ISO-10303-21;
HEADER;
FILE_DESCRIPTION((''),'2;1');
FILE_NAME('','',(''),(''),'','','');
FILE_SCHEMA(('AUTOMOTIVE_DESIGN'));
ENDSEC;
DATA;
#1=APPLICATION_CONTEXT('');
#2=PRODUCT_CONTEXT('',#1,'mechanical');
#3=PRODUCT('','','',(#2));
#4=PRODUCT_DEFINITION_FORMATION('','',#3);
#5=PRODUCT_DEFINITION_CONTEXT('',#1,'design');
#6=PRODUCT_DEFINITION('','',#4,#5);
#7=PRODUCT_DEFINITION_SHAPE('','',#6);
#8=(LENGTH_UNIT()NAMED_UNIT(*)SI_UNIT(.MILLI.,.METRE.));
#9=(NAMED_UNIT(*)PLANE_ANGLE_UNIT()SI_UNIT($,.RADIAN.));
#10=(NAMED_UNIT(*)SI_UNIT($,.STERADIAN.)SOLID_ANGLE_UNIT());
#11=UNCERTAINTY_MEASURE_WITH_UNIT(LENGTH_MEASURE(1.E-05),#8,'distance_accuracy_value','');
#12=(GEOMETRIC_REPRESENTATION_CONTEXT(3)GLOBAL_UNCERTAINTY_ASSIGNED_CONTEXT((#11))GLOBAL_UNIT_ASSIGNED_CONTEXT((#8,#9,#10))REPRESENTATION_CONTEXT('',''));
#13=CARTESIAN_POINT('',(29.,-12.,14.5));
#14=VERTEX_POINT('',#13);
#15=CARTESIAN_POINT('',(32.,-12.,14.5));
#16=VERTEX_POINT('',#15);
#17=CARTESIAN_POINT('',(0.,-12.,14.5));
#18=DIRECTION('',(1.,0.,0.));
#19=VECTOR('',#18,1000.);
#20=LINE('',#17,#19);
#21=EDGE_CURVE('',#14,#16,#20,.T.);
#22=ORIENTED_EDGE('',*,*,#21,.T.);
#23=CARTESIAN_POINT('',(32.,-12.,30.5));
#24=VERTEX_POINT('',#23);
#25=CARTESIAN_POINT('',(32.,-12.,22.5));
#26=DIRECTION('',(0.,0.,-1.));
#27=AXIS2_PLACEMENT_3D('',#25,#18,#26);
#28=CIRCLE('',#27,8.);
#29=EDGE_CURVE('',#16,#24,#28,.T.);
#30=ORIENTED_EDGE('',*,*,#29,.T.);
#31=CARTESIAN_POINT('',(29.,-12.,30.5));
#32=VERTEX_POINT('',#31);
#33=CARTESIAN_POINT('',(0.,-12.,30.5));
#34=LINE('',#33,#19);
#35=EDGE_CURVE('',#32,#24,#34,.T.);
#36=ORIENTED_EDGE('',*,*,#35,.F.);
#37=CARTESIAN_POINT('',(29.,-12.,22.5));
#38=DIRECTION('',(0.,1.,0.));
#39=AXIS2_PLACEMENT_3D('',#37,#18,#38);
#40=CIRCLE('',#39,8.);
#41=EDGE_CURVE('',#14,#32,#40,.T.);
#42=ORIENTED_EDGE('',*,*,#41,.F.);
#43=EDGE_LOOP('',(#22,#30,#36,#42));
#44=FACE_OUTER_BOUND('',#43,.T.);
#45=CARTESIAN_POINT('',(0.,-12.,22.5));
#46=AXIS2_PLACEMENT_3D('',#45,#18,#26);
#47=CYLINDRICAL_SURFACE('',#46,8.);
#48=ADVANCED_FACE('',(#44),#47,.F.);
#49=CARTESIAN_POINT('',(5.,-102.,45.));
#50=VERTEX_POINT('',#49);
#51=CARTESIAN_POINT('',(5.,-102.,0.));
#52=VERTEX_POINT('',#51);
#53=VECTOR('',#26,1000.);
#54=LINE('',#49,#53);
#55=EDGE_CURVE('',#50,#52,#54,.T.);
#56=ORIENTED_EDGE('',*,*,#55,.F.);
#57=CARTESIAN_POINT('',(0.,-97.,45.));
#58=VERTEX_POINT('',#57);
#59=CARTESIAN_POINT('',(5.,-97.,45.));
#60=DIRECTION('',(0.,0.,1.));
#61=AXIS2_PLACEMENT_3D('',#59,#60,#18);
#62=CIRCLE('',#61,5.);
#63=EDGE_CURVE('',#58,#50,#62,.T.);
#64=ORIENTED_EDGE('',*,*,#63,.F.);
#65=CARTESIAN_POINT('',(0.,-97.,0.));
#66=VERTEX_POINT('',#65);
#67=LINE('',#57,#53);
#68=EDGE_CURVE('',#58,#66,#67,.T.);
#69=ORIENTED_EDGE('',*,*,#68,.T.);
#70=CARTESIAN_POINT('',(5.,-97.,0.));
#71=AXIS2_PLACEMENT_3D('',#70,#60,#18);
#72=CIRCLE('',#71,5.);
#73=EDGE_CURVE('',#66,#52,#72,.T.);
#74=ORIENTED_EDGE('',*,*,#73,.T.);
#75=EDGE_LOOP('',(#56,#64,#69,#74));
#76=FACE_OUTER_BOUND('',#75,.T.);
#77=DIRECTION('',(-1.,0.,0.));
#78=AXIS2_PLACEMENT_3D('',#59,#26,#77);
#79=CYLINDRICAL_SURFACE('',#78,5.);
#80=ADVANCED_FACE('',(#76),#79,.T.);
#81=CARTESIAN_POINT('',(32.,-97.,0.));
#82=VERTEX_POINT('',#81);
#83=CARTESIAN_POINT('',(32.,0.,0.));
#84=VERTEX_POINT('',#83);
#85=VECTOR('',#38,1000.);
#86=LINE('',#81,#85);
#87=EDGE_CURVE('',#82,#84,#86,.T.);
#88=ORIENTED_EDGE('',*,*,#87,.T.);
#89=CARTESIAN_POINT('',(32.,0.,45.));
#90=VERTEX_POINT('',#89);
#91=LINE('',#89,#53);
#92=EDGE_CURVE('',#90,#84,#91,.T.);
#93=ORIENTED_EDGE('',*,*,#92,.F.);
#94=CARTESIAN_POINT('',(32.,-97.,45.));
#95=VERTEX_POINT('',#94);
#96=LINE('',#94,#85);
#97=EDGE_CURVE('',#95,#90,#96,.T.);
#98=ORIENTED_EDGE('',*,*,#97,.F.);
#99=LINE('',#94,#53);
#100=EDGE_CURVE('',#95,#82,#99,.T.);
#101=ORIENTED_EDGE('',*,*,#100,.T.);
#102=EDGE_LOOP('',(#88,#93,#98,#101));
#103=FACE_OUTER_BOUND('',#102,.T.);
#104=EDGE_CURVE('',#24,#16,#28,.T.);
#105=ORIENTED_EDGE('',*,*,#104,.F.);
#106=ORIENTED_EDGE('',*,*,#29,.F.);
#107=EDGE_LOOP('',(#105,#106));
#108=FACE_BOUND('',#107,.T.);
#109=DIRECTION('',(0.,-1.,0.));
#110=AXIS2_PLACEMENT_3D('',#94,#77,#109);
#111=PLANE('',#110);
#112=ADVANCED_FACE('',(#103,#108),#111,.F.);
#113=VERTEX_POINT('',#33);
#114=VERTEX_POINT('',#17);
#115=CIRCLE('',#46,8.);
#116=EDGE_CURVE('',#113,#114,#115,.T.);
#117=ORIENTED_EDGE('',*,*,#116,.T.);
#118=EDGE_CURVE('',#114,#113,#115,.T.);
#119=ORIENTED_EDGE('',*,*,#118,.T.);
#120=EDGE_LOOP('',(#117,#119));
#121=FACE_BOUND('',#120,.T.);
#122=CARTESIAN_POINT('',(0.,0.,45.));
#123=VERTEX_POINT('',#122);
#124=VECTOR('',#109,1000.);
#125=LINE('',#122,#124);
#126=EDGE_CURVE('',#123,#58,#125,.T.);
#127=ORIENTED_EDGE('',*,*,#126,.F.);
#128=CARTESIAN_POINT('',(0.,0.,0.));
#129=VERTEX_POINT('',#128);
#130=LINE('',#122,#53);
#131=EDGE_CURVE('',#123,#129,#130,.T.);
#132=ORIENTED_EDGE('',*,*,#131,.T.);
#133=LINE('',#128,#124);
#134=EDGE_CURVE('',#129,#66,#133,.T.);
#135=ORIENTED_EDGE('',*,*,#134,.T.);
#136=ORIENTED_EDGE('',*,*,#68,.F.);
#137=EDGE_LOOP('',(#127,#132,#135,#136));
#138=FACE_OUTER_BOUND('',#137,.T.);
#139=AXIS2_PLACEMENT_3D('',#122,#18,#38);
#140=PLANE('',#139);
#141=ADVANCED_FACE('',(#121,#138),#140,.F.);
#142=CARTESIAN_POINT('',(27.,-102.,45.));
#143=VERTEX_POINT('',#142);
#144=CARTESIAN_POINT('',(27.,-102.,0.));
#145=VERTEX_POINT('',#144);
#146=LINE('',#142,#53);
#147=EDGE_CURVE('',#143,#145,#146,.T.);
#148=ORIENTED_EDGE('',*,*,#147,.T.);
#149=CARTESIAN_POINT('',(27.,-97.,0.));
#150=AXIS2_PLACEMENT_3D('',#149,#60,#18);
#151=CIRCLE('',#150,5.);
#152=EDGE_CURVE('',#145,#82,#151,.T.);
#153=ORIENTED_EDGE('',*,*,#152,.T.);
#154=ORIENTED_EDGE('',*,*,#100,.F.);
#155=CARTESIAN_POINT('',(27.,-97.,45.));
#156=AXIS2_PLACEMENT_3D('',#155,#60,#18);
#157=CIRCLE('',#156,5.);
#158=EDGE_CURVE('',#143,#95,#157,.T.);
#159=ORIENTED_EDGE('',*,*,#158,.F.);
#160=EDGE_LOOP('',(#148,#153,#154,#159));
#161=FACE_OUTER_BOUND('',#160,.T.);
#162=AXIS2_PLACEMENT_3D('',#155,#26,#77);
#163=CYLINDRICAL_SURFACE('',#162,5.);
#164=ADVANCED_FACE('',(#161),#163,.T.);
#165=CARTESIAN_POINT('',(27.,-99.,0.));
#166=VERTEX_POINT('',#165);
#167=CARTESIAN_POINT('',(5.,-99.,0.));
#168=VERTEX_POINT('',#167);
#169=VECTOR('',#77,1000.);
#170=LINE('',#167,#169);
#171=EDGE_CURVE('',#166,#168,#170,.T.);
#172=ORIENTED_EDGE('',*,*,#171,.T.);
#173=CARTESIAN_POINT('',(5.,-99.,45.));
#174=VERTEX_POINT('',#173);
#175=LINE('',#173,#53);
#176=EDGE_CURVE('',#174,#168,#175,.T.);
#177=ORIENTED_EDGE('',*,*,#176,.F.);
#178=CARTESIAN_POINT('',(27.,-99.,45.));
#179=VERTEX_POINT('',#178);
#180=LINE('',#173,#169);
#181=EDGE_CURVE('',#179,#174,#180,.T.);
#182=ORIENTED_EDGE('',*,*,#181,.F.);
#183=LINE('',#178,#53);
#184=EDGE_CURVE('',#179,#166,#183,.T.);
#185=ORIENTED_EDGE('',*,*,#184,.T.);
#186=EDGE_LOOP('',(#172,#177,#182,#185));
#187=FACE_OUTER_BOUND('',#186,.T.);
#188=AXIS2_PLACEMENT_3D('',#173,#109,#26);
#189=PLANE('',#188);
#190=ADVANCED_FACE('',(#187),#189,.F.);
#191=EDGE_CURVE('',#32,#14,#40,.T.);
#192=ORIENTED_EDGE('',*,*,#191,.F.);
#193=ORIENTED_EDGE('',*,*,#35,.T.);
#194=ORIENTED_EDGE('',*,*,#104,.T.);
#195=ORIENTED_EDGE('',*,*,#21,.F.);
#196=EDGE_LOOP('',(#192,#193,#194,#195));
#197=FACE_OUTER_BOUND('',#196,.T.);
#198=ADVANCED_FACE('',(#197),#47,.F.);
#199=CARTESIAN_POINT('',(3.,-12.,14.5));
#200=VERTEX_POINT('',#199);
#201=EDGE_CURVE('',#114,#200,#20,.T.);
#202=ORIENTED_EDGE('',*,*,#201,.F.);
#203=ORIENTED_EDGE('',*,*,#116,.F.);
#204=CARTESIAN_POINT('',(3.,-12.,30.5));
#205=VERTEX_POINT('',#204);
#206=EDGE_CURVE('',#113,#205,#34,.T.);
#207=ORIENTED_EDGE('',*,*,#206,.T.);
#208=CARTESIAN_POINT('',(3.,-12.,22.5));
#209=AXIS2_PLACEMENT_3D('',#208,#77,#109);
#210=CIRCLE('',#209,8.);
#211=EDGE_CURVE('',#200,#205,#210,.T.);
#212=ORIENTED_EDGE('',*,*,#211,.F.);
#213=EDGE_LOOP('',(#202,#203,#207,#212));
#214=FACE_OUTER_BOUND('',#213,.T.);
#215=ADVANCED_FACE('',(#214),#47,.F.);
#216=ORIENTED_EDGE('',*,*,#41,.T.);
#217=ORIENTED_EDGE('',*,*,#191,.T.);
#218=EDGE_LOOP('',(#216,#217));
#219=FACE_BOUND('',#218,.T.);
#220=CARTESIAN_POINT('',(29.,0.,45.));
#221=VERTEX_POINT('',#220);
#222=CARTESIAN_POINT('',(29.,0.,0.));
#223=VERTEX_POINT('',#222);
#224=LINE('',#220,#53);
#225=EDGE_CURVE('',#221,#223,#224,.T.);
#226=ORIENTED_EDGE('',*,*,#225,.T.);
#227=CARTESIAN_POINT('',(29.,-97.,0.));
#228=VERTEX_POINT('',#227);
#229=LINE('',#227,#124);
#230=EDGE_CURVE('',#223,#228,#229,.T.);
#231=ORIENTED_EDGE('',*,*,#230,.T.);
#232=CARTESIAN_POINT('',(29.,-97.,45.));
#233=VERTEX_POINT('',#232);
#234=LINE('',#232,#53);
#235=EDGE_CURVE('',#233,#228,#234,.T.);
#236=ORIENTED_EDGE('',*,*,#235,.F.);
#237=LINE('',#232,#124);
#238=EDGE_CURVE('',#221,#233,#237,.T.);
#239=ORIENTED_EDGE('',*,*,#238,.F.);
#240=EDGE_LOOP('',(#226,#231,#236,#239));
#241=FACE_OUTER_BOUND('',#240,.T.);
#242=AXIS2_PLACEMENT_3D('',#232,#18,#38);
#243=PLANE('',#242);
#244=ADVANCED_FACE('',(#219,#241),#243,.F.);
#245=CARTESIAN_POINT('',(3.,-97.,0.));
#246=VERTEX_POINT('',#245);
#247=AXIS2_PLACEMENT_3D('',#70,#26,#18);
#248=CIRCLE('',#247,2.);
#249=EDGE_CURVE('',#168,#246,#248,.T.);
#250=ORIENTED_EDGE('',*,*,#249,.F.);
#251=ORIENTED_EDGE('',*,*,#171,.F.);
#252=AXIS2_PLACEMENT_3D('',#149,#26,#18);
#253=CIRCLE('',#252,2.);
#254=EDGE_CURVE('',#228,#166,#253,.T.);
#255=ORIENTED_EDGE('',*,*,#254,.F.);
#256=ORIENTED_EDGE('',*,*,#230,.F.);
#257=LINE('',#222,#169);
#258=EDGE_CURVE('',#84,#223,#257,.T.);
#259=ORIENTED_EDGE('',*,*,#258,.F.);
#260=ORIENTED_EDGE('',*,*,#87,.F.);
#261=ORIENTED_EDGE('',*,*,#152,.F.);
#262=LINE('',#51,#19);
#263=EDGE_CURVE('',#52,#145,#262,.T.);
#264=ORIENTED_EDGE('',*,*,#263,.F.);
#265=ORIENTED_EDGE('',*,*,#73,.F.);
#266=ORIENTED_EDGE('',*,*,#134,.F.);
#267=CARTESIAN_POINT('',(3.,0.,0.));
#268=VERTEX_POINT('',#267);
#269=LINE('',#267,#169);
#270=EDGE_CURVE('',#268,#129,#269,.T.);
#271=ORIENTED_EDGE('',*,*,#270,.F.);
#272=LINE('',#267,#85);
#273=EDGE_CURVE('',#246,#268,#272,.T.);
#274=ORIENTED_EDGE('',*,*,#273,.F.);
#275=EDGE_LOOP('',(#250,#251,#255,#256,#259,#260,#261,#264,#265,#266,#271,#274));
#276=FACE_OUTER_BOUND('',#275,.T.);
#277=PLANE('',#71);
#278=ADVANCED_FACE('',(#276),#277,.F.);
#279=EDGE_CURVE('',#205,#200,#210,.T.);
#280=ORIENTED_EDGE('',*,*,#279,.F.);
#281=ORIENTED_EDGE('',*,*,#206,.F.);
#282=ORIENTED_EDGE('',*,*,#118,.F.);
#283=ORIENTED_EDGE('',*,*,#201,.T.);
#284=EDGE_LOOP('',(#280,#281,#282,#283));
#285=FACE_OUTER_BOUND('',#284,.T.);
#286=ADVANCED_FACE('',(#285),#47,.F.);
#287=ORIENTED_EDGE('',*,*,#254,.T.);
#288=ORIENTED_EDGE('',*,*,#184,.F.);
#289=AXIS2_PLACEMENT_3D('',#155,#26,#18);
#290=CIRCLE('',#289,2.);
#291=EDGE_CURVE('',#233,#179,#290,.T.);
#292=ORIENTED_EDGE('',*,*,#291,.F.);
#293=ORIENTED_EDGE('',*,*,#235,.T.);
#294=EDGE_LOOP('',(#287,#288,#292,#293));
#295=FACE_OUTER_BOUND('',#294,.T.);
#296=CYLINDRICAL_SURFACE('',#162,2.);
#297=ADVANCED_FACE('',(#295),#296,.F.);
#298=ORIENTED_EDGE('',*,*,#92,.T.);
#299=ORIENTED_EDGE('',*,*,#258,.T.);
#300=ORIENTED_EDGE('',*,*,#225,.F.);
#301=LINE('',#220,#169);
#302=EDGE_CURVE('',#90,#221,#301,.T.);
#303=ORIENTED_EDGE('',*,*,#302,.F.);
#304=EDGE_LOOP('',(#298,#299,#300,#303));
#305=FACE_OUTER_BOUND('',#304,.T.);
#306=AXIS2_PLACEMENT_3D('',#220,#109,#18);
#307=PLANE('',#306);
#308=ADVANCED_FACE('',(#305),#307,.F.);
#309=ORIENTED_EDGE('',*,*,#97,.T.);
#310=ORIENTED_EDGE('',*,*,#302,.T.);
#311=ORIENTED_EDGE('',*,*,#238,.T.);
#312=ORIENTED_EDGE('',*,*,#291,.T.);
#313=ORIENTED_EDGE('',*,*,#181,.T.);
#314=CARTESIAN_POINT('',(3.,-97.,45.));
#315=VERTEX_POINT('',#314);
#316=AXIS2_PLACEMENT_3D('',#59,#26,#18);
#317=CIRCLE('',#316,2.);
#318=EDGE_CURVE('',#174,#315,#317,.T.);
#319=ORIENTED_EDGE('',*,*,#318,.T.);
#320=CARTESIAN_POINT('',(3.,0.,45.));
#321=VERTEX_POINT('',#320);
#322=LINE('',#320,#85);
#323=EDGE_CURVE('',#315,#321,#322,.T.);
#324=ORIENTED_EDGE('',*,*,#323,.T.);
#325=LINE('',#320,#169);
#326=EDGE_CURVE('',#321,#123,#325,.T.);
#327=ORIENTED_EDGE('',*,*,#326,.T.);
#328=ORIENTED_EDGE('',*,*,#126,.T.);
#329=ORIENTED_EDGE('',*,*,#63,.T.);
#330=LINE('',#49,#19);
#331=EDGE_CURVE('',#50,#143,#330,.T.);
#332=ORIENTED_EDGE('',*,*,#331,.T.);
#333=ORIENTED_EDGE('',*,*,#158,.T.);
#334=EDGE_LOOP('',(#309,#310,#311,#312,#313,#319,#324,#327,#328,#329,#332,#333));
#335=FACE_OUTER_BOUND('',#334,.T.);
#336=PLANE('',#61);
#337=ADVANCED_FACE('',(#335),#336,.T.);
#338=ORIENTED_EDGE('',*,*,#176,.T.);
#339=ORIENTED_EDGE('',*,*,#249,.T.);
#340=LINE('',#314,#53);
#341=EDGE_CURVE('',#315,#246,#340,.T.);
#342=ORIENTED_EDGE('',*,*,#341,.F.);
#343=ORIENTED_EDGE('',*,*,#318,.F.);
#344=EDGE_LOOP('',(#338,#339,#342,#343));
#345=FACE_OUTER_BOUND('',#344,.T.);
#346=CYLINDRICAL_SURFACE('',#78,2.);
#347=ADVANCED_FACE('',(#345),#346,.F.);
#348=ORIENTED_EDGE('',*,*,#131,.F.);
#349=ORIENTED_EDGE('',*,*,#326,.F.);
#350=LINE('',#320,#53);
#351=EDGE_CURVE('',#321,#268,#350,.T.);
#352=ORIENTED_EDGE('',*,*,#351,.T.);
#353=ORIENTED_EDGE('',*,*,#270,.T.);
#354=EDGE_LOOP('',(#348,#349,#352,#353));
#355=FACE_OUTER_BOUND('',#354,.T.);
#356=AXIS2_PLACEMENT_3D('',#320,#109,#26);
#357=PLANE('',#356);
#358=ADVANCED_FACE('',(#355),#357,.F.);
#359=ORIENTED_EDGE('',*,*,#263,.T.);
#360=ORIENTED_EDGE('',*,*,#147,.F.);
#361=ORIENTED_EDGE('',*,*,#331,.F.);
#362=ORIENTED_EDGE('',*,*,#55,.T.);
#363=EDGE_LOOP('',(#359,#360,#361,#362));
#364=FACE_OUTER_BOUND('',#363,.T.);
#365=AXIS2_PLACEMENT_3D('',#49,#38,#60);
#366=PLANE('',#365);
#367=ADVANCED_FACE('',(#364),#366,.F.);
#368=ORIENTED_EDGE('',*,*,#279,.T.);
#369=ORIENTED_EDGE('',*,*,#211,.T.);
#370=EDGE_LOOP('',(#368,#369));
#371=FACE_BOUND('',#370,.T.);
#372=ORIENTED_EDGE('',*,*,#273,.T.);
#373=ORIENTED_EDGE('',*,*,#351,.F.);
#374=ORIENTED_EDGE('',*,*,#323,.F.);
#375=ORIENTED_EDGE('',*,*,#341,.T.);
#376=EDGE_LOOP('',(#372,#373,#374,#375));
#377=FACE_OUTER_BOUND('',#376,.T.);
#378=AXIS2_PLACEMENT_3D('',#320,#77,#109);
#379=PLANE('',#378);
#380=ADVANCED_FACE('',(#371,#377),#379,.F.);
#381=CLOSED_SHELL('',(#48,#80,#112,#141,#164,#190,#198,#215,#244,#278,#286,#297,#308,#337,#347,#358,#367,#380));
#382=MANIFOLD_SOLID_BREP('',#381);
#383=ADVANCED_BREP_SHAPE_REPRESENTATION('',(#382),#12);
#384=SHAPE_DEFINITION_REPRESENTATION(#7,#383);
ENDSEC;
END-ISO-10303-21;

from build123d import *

# Parameters (mm, degrees)
BOSS_EXTRUDE1_DEPTH = 45
SKETCH2_R           = 8
CUT_EXTRUDE1_DEPTH  = 116.987068245


with BuildPart() as part:
    # Sketch1 → Boss-Extrude1 (new body)
    with BuildSketch(Plane.XY):
        with BuildLine():
            Line((0, 0), (0, -97))
            ThreePointArc((0, -97), (1.464466094, -100.535533906), (5, -102))
            Line((5, -102), (27, -102))
            ThreePointArc((27, -102), (30.535533906, -100.535533906), (32, -97))
            Line((32, -97), (32, 0))
            Line((32, 0), (29, 0))
            Line((29, 0), (29, -97))
            ThreePointArc((29, -97), (28.414213562, -98.414213562), (27, -99))
            Line((27, -99), (5, -99))
            ThreePointArc((5, -99), (3.585786438, -98.414213562), (3, -97))
            Line((3, -97), (3, 0))
            Line((3, 0), (0, 0))
        make_face()
    extrude(amount=BOSS_EXTRUDE1_DEPTH)

    # Sketch2 → Cut-Extrude1 (cut, through all)
    with BuildSketch(Plane(origin=(32, 0, 0), x_dir=(0, 0, -1), z_dir=(1, 0, 0))):
        with Locations((-22.5, -12)):
            Circle(SKETCH2_R)
    extrude(amount=-CUT_EXTRUDE1_DEPTH, mode=Mode.SUBTRACT)


solid = part.part
